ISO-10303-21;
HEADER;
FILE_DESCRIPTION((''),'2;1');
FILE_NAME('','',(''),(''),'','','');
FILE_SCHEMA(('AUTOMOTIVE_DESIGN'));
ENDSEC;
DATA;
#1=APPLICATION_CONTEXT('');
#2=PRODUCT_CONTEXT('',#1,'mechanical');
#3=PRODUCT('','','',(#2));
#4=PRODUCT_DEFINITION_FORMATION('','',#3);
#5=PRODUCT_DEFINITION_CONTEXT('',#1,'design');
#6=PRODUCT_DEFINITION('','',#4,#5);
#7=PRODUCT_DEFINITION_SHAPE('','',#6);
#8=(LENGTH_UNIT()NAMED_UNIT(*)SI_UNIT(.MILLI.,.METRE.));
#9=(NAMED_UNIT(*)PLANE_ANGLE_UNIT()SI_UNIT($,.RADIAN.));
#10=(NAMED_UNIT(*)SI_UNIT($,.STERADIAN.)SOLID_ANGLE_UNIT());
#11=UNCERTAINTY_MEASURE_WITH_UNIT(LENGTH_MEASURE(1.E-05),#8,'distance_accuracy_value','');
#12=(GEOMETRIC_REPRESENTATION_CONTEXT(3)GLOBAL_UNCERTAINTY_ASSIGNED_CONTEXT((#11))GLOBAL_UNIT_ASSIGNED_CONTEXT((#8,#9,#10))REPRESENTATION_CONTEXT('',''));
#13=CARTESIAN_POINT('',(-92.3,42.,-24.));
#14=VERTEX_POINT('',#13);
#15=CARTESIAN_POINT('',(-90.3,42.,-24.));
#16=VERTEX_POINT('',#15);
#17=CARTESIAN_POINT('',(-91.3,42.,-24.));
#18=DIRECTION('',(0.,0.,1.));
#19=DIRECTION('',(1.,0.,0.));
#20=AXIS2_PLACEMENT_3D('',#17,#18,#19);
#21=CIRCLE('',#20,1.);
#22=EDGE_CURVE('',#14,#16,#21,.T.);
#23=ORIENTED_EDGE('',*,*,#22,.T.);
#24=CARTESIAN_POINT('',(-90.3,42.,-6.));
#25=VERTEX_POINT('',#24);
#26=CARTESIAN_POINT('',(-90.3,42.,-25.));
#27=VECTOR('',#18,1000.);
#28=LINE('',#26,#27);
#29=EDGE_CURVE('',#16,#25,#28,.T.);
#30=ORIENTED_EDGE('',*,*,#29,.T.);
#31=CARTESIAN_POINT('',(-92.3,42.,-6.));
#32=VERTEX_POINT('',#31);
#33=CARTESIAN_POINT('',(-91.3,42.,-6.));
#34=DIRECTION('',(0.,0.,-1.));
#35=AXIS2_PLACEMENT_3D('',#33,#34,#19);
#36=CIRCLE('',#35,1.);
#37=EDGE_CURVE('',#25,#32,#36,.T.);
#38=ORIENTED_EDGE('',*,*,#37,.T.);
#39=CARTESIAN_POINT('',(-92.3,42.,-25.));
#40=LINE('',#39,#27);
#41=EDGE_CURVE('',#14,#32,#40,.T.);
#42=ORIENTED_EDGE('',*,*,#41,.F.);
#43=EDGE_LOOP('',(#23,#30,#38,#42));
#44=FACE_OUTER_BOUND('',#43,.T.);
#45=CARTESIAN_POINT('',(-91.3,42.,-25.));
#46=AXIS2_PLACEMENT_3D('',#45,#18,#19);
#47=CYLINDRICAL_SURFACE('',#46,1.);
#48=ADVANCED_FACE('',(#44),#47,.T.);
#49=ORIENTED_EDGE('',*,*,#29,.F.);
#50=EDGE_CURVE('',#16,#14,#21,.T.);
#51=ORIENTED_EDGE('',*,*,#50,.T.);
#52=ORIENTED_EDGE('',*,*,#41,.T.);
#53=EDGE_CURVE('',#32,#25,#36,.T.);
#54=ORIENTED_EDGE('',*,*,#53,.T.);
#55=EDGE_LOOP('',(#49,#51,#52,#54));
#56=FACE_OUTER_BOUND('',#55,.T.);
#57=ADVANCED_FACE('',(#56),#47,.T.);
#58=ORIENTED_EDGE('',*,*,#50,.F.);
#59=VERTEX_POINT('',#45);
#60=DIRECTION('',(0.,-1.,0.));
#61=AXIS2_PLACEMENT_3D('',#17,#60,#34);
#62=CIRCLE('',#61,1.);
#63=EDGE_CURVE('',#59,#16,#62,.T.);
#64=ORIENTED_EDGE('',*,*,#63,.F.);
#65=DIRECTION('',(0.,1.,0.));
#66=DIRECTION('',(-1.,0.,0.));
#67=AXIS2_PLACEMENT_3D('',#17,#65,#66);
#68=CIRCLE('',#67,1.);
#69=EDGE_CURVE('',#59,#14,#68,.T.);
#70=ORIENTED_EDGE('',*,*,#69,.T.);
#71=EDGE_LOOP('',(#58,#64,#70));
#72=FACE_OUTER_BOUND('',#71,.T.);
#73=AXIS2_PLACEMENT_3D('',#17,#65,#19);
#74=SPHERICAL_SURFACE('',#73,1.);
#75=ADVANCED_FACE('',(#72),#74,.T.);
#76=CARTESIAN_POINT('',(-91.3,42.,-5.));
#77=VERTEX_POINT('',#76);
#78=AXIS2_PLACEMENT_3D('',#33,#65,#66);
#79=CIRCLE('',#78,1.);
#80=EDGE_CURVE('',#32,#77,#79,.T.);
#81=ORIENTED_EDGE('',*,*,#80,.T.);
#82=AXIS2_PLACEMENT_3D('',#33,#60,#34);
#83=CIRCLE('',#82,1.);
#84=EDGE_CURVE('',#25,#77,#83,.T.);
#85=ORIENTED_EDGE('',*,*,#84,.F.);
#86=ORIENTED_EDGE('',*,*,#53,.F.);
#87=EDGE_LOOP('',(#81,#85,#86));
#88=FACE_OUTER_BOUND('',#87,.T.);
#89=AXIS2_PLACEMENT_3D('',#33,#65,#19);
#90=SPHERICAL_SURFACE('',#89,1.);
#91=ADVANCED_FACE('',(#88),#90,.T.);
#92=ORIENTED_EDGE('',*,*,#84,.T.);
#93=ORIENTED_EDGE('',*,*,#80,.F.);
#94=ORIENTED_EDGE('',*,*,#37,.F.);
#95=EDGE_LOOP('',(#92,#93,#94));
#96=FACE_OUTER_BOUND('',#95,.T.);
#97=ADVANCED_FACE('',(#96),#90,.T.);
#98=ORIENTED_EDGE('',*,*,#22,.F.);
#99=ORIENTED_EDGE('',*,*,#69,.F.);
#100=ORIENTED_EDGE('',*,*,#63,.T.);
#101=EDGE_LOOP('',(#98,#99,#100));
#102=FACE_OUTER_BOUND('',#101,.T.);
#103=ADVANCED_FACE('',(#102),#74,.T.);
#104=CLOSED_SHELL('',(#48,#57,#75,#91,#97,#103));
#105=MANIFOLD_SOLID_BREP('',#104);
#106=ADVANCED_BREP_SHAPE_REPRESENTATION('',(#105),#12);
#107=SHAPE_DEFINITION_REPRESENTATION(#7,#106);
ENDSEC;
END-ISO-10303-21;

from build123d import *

# Parameters (mm, degrees)
BOSS_EXTRUDE1_START = -15
SKETCH1_R           = 1
BOSS_EXTRUDE1_DEPTH = 10
FILLET1_R           = 1


with BuildPart() as part:
    # Sketch1 → Boss-Extrude1 (new, symmetric)
    with BuildSketch(Plane.XY.offset(BOSS_EXTRUDE1_START)):
        with Locations((-91.3, 42)):
            Circle(SKETCH1_R)
    extrude(amount=BOSS_EXTRUDE1_DEPTH, both=True)

    # Fillet1
    fillet1_edges = [part.edges().sort_by_distance(p)[0] for p in [
        (-92.3, 42, -5),
        (-92.3, 42, -25),
    ]]
    fillet(fillet1_edges, radius=FILLET1_R)


solid = part.part
